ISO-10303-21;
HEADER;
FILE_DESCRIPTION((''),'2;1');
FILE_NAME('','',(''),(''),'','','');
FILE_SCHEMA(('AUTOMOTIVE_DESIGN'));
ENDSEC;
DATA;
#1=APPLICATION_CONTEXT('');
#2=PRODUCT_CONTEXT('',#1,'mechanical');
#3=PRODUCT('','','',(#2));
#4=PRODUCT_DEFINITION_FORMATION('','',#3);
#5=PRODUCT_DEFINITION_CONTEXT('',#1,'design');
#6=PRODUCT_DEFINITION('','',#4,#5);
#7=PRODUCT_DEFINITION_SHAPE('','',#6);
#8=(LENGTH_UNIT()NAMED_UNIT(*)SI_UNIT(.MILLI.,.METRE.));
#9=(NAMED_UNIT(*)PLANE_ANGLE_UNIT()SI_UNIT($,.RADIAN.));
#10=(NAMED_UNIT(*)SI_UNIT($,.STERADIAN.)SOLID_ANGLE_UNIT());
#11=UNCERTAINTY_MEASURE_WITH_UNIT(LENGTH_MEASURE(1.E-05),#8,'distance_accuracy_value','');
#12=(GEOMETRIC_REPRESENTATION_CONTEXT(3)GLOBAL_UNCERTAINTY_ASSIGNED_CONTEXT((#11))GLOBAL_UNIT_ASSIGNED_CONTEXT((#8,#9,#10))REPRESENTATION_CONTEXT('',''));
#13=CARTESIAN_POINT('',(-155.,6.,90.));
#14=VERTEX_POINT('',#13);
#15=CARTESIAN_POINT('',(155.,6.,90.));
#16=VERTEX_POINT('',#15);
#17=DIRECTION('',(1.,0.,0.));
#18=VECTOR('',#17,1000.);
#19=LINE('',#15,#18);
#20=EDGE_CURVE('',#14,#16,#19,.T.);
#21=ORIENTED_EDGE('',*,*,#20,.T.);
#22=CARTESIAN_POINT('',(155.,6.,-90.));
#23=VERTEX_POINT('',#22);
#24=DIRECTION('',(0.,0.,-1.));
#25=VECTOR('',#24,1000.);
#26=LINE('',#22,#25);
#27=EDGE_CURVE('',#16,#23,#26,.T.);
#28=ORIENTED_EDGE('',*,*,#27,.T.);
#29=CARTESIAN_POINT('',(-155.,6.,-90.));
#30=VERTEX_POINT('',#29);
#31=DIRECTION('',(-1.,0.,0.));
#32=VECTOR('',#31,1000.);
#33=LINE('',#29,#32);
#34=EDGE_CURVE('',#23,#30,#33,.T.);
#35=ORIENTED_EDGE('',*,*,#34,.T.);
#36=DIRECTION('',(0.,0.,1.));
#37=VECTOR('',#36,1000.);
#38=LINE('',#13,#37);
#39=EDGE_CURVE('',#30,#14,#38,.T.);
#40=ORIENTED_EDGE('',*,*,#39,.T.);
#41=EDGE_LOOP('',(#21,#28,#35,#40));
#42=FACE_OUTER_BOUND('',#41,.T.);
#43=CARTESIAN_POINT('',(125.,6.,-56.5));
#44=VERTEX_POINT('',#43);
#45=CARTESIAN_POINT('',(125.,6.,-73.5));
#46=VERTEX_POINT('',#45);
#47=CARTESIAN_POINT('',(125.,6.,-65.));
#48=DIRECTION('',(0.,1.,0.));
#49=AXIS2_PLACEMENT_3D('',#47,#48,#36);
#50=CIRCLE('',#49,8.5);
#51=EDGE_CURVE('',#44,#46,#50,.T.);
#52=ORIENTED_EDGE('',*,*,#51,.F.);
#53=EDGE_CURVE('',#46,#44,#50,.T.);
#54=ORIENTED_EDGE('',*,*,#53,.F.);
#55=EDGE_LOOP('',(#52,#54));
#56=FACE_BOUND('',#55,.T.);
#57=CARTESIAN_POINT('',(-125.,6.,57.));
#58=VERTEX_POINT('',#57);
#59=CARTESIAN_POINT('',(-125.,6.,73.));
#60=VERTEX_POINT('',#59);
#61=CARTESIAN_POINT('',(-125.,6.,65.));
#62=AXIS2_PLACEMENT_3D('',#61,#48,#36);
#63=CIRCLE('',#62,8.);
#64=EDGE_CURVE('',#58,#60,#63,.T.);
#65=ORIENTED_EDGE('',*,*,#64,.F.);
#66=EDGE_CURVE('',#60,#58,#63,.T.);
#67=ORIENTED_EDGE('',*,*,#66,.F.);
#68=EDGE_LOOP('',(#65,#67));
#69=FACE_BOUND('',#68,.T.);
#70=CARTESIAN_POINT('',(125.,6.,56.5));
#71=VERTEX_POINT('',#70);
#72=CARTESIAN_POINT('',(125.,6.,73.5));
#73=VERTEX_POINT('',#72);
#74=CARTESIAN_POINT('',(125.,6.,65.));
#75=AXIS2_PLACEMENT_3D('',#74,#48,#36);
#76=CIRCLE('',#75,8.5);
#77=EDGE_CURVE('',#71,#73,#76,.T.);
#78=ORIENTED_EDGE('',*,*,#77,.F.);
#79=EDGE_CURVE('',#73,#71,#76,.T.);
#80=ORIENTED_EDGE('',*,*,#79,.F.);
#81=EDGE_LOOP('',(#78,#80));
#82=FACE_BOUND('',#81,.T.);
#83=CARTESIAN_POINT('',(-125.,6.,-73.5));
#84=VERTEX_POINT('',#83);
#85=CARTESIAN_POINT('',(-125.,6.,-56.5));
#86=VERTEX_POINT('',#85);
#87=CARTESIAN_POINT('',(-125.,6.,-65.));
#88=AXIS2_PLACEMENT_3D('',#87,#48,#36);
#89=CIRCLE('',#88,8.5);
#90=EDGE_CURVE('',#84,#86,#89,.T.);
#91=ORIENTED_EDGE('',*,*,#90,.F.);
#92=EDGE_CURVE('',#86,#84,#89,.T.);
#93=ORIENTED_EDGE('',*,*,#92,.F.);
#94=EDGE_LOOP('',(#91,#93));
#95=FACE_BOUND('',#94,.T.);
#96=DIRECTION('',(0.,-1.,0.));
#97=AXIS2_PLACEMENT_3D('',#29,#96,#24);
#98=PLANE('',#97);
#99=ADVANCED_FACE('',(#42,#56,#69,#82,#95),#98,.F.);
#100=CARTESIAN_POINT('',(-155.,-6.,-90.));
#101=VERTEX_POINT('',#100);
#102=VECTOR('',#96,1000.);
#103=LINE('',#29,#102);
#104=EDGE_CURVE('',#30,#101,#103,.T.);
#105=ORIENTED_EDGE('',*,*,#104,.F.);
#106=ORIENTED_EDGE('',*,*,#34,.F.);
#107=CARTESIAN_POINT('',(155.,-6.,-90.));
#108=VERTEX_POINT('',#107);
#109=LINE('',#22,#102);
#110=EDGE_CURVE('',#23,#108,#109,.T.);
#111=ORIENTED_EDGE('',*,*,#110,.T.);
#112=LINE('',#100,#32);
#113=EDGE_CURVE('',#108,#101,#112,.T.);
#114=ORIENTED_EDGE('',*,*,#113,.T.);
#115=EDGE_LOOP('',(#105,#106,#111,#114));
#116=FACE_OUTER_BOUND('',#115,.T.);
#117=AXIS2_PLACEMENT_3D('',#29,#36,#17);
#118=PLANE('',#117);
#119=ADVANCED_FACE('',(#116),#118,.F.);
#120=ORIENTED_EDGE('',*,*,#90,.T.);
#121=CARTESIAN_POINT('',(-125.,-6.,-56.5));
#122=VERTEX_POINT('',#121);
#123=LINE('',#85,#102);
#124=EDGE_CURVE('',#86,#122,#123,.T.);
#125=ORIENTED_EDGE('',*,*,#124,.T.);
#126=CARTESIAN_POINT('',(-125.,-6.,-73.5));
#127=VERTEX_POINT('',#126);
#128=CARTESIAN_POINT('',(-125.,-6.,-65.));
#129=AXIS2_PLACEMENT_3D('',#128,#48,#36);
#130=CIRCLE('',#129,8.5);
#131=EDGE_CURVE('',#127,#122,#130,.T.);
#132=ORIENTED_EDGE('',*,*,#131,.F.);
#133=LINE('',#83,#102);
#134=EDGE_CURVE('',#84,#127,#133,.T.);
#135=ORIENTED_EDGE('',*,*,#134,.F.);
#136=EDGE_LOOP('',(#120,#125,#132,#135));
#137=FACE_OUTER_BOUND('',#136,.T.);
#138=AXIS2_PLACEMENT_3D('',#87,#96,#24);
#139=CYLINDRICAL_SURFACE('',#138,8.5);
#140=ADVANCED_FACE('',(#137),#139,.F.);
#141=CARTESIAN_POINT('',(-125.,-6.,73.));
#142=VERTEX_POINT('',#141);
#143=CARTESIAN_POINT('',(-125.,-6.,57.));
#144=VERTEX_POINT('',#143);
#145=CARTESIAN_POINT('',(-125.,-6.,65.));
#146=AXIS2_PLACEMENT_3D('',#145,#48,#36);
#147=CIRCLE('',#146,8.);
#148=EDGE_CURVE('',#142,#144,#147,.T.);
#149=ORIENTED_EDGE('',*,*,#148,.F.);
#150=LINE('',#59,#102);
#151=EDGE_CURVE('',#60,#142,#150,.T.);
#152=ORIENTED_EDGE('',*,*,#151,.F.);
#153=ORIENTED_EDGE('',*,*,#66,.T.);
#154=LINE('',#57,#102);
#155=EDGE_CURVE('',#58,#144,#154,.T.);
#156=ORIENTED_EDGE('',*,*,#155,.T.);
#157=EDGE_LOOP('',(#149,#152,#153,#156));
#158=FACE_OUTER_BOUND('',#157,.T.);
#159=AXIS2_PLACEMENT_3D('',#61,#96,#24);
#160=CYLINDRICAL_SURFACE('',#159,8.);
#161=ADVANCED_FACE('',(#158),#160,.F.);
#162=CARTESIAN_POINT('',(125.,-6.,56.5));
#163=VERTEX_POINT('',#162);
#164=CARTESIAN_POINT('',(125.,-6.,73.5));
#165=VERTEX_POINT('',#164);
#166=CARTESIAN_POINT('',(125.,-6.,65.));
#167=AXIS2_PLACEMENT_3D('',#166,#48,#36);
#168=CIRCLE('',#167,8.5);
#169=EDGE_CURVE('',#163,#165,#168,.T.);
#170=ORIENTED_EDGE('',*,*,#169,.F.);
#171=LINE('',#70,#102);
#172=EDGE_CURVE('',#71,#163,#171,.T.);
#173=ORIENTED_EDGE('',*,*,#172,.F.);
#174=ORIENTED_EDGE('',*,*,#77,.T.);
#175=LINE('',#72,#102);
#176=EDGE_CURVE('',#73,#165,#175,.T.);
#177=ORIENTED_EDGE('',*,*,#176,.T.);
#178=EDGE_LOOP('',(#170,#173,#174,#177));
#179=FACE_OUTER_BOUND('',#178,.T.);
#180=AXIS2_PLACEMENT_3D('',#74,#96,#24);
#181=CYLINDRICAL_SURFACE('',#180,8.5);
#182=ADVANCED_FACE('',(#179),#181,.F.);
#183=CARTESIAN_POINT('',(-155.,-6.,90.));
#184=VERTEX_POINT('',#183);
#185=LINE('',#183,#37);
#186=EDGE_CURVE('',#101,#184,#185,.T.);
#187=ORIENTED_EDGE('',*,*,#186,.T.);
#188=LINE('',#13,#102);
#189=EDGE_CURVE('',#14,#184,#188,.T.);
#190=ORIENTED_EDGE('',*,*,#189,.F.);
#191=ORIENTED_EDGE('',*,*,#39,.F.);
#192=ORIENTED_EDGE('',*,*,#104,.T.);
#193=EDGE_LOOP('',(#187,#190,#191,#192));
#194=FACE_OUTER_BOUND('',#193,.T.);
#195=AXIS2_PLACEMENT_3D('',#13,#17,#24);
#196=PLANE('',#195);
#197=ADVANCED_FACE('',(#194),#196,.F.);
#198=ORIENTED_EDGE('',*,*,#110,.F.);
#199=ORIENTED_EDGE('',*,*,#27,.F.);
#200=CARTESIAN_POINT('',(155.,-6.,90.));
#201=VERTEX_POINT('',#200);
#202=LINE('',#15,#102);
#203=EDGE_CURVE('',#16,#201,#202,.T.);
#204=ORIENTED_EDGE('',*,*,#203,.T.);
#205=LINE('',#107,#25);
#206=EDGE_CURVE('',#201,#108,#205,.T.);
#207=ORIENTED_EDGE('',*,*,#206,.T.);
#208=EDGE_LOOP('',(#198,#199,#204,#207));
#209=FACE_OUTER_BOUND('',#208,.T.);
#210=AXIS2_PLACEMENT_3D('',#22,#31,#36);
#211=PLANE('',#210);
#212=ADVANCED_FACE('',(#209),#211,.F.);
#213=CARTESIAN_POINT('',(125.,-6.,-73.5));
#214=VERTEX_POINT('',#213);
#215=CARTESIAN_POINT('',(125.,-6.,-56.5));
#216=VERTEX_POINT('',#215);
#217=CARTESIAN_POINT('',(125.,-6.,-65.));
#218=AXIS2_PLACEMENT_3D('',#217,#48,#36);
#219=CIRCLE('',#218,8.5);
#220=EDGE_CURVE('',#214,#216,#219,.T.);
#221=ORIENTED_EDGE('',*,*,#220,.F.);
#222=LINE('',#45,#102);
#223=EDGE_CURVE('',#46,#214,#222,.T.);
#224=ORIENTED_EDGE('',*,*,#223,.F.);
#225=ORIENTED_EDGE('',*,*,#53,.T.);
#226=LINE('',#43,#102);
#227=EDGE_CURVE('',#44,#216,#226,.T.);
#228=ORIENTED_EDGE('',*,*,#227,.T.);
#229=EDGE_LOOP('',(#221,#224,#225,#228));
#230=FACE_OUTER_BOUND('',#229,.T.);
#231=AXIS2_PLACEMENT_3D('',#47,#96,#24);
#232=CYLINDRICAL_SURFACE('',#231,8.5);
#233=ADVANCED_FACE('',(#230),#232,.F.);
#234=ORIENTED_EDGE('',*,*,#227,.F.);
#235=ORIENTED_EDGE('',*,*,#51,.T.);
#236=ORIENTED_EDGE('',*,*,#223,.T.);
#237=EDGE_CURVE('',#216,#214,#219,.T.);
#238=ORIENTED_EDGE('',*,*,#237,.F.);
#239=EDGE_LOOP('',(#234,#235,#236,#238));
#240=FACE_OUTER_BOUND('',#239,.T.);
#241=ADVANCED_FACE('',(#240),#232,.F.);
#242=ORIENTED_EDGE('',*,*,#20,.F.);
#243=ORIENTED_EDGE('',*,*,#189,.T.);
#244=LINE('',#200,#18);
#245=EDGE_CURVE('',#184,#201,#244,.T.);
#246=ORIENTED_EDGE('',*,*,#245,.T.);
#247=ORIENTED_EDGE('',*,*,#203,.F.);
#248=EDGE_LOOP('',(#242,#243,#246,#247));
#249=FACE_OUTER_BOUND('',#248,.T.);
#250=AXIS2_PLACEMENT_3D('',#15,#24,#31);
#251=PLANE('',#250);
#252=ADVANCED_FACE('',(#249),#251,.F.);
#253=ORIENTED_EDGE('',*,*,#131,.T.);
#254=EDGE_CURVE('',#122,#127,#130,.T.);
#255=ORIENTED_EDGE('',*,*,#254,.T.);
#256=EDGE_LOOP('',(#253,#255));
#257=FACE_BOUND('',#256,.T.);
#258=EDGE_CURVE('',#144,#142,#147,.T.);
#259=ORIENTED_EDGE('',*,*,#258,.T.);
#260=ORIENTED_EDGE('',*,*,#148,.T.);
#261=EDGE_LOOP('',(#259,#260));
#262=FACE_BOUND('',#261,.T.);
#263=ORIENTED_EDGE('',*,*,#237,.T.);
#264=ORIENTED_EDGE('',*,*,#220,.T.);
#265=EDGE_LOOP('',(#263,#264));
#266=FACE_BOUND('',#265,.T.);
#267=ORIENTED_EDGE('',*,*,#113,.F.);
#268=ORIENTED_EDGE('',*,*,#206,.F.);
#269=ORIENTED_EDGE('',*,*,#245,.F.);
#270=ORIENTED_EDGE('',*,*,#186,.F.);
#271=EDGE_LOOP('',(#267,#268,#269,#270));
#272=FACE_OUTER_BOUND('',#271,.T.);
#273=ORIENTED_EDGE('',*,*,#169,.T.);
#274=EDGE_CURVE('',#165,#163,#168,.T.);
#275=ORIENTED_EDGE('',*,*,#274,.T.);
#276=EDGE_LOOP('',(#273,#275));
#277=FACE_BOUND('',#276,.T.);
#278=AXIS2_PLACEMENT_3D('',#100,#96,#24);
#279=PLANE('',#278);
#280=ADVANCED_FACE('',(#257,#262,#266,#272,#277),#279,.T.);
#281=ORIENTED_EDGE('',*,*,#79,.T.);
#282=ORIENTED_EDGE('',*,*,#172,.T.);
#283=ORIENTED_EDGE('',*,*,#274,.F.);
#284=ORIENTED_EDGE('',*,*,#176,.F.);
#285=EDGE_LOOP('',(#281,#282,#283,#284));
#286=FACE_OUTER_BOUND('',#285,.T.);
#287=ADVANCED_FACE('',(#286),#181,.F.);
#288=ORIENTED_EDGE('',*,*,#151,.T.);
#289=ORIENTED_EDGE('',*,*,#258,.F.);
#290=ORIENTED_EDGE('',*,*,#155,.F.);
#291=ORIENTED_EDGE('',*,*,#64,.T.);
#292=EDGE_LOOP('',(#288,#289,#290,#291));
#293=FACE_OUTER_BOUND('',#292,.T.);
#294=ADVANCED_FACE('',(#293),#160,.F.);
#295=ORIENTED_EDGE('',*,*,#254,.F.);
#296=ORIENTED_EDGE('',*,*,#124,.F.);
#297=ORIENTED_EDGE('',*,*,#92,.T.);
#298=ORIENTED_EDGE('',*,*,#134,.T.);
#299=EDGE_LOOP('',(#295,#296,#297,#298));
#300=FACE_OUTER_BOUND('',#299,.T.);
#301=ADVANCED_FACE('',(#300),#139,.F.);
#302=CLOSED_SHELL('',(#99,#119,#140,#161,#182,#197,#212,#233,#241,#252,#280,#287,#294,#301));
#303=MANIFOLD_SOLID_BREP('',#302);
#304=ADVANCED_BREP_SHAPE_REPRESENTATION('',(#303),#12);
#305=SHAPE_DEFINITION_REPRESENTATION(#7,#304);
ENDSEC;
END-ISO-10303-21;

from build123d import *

# Parameters (mm, degrees)
SKETCH1_W      = 310
SKETCH1_H      = 180
SKETCH1_R      = 8.5
SKETCH1_R_2    = 8
EXTRUDE1_DEPTH = 6


with BuildPart() as part:
    # Sketch1 → Extrude1 (new, symmetric)
    with BuildSketch(Plane(origin=(0, 0, 0), x_dir=(1, 0, 0), z_dir=(0, 1, 0))):
        Rectangle(SKETCH1_W, SKETCH1_H)
        with Locations(Location((125, -65, 0), (0, 0, 270))):
            Circle(SKETCH1_R, mode=Mode.SUBTRACT)
        with Locations(Location((-125, -65, 0), (0, 0, 270))):
            Circle(SKETCH1_R_2, mode=Mode.SUBTRACT)
        with Locations(Location((-125, 65, 0), (0, 0, 270))):
            Circle(SKETCH1_R, mode=Mode.SUBTRACT)
        with Locations(Location((125, 65, 0), (0, 0, 270))):
            Circle(SKETCH1_R, mode=Mode.SUBTRACT)
    extrude(amount=EXTRUDE1_DEPTH, both=True)


solid = part.part
